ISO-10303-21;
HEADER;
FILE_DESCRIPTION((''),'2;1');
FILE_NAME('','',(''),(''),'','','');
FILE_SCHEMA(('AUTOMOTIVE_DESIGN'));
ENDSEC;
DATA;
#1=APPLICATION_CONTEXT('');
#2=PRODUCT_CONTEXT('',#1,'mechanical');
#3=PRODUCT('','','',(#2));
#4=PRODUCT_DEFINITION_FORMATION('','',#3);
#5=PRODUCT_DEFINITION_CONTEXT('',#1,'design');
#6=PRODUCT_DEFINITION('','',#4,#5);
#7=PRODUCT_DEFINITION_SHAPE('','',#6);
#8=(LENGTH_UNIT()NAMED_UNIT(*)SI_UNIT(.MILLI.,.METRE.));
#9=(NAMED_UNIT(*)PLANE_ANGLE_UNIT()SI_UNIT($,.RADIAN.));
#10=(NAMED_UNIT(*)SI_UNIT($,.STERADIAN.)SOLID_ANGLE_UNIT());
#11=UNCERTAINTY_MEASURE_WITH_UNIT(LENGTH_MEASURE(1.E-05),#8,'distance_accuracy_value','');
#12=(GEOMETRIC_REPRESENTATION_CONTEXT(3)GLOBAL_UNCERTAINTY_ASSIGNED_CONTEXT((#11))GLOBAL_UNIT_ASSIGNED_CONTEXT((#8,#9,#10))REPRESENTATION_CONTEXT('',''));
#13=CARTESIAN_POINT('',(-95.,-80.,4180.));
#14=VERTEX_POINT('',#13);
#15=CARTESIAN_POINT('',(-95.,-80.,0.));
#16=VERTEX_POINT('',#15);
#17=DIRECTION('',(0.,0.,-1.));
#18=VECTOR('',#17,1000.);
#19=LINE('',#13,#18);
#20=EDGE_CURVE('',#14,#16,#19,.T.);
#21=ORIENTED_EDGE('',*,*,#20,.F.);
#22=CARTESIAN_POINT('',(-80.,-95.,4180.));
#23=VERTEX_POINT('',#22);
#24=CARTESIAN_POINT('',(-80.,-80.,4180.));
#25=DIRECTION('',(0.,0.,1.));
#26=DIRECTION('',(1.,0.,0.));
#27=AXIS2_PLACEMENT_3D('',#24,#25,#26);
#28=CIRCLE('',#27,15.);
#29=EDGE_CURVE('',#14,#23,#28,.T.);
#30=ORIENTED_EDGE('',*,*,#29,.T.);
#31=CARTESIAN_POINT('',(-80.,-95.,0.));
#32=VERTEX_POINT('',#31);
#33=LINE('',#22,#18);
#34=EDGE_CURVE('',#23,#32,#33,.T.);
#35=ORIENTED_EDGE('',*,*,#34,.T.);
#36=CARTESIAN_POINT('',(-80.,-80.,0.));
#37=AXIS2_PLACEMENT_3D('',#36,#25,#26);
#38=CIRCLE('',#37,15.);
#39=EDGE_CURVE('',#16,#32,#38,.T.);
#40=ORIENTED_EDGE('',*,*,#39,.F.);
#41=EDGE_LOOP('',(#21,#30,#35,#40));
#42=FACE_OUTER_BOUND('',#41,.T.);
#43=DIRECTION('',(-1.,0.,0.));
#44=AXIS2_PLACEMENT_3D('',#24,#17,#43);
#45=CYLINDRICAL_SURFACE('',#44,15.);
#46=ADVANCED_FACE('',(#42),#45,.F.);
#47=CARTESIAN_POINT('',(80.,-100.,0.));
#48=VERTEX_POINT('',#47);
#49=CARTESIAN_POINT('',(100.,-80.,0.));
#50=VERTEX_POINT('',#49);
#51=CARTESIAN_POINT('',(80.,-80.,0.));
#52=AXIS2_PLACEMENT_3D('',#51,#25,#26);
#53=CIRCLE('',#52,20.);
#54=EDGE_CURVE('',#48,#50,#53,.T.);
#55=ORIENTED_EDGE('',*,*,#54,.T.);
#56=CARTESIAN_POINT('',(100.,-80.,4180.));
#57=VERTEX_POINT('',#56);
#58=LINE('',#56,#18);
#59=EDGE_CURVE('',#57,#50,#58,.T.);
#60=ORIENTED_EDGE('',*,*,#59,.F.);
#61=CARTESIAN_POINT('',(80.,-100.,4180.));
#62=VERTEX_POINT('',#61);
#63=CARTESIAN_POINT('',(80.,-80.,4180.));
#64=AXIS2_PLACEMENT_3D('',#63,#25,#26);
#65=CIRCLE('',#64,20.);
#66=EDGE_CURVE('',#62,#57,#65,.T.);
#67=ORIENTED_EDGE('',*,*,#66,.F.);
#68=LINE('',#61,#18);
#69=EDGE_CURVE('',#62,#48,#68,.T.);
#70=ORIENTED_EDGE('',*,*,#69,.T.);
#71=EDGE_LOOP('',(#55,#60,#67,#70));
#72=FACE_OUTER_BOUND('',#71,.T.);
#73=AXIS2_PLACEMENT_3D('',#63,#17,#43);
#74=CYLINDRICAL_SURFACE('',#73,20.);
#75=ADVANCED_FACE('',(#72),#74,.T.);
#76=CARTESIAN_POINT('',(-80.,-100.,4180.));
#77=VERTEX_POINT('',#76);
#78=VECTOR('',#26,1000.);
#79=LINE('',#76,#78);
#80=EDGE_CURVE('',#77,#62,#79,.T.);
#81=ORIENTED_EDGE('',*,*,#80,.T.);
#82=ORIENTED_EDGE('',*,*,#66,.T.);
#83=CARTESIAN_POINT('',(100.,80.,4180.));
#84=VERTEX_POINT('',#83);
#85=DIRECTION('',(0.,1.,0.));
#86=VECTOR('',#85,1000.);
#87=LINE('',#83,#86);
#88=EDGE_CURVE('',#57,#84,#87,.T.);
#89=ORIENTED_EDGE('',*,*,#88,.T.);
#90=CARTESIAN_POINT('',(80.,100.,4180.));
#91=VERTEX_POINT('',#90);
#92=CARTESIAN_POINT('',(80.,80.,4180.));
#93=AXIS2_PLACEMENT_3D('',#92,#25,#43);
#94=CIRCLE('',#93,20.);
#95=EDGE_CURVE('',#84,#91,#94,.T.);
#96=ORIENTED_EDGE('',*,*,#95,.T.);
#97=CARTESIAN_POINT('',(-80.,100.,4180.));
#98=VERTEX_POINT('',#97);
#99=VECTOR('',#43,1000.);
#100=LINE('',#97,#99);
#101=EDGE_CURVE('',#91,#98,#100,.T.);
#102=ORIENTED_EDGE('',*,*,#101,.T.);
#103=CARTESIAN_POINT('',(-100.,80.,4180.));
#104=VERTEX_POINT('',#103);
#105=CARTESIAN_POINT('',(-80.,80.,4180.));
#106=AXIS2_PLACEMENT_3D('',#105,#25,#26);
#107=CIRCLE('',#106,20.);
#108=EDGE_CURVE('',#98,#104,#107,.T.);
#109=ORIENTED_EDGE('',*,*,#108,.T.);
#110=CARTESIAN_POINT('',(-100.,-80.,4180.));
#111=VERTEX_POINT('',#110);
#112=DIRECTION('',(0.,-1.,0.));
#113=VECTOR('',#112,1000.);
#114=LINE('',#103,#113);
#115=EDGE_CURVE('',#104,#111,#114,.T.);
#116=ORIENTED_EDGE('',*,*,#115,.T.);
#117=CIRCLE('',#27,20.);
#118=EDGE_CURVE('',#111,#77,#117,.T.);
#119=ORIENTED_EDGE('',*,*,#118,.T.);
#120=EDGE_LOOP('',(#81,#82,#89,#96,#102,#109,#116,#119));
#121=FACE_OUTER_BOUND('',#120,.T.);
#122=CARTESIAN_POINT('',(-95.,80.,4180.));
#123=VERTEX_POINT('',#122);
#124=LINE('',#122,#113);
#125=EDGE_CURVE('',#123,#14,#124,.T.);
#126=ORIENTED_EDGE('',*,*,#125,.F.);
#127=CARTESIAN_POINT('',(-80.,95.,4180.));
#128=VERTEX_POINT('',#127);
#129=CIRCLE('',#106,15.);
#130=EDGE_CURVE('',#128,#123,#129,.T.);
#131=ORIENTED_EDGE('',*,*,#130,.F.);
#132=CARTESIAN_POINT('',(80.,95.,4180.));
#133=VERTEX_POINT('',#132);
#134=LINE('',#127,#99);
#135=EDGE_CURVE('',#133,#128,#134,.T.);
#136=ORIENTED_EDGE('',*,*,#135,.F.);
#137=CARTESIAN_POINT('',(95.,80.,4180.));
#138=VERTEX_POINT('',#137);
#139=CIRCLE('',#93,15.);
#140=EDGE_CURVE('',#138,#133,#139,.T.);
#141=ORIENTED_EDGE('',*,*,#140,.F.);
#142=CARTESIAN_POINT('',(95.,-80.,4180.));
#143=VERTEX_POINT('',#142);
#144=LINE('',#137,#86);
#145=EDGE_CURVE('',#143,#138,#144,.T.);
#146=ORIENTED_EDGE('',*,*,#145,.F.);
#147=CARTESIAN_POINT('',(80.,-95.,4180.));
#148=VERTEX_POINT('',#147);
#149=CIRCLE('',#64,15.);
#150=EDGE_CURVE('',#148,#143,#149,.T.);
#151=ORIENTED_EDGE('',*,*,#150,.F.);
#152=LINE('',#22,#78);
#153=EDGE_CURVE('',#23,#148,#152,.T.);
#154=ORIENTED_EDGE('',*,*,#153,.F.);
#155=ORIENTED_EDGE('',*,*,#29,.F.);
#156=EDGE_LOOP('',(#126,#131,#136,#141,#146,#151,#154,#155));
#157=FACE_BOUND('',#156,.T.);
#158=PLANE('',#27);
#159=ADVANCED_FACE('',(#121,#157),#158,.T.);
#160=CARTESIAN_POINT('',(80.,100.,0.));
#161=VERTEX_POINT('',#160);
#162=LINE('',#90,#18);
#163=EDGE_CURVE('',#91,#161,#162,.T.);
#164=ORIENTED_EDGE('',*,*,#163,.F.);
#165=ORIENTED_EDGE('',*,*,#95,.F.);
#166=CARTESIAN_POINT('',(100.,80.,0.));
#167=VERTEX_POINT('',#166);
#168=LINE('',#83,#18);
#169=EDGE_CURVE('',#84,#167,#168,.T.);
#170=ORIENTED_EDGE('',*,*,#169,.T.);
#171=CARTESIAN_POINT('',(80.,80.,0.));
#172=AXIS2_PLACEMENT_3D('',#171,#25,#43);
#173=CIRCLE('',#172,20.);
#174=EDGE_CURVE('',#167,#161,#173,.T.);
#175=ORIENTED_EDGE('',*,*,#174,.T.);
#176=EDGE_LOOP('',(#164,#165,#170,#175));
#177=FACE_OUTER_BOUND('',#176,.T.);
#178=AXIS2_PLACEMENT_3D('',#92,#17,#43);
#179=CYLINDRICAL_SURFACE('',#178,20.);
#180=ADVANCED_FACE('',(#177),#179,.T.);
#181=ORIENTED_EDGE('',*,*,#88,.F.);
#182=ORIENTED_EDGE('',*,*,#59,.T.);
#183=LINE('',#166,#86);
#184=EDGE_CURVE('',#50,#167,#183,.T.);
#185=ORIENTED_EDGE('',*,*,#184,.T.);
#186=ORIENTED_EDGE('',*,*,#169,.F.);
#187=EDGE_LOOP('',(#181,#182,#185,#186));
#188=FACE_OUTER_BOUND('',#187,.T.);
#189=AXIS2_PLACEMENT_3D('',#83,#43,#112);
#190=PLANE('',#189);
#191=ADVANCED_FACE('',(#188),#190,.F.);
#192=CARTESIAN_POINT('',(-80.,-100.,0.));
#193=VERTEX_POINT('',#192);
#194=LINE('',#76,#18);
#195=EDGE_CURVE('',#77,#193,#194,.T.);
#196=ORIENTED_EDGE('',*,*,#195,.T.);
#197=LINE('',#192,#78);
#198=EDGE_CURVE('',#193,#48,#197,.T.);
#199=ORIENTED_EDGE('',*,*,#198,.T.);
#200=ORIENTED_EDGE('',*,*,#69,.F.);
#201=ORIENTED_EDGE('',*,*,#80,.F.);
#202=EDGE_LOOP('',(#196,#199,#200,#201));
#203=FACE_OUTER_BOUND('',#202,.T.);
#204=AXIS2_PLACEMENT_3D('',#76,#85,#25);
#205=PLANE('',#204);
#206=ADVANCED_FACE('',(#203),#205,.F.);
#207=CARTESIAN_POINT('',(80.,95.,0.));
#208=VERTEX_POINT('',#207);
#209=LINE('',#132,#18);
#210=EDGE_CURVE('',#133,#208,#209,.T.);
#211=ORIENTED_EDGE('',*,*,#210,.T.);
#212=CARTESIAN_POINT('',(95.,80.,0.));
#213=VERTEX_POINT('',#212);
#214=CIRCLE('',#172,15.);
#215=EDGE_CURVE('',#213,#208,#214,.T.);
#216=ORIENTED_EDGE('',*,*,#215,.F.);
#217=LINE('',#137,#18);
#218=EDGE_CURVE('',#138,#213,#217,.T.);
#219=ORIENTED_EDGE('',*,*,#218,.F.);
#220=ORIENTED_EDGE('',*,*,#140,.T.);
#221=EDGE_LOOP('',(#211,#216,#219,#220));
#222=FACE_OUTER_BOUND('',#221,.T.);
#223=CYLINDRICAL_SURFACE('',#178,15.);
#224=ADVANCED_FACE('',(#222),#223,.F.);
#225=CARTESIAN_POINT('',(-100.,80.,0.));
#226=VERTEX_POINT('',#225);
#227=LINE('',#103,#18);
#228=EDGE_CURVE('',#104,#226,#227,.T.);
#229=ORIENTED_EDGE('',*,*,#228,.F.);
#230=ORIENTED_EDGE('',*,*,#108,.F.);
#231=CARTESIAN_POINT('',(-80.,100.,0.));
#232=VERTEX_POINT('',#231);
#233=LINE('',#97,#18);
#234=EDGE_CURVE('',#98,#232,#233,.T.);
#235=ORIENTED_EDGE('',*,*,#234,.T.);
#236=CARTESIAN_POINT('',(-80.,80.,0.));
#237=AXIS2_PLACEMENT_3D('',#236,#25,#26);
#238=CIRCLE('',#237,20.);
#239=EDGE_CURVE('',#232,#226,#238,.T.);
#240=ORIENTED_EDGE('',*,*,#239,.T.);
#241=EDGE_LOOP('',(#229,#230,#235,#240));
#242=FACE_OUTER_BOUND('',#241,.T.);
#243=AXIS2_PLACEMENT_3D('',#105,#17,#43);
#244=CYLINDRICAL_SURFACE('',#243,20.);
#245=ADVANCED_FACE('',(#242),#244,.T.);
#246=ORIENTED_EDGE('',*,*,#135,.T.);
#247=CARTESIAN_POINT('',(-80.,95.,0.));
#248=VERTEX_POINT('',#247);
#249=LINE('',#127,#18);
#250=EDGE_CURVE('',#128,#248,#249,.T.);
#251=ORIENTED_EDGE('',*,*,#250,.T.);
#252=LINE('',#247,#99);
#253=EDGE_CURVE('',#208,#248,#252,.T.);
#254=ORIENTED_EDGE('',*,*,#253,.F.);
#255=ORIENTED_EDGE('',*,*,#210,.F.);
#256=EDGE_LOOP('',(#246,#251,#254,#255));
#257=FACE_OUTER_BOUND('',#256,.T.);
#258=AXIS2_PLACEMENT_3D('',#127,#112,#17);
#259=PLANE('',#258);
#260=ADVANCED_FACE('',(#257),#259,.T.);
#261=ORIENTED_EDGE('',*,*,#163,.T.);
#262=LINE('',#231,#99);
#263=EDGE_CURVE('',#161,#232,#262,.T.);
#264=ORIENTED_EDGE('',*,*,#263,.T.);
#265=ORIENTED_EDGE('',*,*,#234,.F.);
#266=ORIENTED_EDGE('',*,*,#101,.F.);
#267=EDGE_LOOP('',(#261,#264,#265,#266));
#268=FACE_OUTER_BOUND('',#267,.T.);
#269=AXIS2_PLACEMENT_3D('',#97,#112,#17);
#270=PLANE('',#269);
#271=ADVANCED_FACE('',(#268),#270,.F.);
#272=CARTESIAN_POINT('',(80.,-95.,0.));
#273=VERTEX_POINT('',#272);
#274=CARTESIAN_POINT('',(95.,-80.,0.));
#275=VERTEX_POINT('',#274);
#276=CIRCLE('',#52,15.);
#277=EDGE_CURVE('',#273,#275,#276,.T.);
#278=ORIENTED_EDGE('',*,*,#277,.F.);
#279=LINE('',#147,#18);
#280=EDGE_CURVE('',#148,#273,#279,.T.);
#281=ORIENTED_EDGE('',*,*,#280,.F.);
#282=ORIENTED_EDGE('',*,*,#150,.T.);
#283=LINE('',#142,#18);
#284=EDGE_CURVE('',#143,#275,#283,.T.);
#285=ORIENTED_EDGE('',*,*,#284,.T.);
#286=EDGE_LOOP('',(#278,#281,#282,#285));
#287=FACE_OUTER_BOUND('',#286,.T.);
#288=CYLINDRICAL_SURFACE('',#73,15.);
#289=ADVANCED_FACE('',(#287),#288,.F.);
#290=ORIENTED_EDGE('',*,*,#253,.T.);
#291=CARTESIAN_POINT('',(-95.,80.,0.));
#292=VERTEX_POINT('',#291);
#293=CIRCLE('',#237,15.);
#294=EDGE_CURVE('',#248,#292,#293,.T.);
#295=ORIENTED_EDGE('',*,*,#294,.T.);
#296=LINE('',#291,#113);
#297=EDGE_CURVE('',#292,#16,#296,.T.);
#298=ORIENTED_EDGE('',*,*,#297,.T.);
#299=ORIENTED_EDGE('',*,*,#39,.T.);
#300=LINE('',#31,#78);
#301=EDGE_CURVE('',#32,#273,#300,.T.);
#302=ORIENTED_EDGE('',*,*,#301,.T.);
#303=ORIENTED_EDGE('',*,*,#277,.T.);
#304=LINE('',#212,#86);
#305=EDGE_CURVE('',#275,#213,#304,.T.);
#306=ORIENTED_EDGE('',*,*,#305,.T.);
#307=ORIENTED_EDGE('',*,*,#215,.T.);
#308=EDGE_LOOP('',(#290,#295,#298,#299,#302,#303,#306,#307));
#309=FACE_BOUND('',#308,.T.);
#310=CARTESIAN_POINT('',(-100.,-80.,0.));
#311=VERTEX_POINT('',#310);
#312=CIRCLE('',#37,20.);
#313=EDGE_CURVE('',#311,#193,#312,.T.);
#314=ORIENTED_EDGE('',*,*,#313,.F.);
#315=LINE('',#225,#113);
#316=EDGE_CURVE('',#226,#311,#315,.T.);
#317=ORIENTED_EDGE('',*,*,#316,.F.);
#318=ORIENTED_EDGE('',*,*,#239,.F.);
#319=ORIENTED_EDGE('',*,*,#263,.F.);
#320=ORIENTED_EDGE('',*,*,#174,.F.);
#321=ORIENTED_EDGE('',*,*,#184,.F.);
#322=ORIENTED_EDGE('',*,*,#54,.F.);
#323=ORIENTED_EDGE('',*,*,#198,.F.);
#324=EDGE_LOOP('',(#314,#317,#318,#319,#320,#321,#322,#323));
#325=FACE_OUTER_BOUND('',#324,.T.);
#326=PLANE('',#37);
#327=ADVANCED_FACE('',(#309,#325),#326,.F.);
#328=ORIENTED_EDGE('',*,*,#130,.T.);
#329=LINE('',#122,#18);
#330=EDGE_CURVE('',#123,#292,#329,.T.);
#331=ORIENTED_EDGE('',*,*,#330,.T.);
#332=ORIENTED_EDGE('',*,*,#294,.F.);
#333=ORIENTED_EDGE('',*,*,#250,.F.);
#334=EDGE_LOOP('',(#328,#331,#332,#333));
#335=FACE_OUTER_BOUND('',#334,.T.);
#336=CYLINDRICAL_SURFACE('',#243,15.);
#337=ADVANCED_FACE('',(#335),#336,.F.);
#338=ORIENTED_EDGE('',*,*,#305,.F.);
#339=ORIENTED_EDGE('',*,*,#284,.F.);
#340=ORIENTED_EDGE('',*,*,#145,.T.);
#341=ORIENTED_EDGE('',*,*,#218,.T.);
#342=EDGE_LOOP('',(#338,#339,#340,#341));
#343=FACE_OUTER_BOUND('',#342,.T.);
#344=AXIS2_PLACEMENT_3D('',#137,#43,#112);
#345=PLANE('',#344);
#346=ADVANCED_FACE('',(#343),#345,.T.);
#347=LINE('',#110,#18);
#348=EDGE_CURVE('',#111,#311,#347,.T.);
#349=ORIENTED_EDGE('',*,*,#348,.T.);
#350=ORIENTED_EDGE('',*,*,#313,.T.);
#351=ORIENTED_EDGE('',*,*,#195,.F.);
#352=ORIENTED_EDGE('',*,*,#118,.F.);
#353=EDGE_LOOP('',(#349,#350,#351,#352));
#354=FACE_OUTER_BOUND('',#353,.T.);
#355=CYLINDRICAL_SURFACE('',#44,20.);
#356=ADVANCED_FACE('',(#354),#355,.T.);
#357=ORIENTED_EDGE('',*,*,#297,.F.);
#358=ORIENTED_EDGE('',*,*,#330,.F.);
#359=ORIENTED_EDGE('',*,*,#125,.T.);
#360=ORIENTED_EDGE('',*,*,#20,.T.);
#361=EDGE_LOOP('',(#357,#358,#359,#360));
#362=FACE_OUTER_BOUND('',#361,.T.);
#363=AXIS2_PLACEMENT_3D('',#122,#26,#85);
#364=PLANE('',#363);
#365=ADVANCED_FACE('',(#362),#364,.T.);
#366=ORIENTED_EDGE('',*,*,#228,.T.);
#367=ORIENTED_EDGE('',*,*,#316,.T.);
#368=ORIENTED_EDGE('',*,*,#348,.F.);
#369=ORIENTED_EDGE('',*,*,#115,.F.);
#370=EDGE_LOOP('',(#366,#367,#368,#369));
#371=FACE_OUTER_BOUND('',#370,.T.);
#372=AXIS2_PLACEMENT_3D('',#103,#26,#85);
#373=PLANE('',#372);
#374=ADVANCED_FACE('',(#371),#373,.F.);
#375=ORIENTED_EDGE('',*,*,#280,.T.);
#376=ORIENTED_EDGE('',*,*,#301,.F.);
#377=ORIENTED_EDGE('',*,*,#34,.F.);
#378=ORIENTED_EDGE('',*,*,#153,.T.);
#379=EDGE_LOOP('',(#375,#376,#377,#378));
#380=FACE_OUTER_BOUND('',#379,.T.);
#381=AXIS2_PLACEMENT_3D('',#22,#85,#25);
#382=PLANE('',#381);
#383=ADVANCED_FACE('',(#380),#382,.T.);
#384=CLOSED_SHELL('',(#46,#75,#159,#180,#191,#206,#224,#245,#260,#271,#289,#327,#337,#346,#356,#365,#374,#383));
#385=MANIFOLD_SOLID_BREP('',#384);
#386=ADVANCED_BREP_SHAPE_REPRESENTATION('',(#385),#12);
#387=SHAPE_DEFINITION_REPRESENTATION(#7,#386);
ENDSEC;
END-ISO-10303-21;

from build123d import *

# Parameters (mm, degrees)
BOSS_EXTRUDE1_DEPTH = 4180


with BuildPart() as part:
    # Sketch1 → Boss-Extrude1 (new body)
    with BuildSketch(Plane.XY):
        with BuildLine():
            Line((-80, 100), (80, 100))
            ThreePointArc((80, 100), (94.142135624, 94.142135624), (100, 80))
            Line((100, 80), (100, -80))
            ThreePointArc((100, -80), (94.142135624, -94.142135624), (80, -100))
            Line((80, -100), (-80, -100))
            ThreePointArc((-80, -100), (-94.142135624, -94.142135624), (-100, -80))
            Line((-100, -80), (-100, 80))
            ThreePointArc((-100, 80), (-94.142135624, 94.142135624), (-80, 100))
        make_face()
        with BuildLine():
            Line((-95, 80), (-95, -80))
            ThreePointArc((-95, -80), (-90.606601718, -90.606601718), (-80, -95))
            Line((-80, -95), (80, -95))
            ThreePointArc((80, -95), (90.606601718, -90.606601718), (95, -80))
            Line((95, -80), (95, 80))
            ThreePointArc((95, 80), (90.606601718, 90.606601718), (80, 95))
            Line((80, 95), (-80, 95))
            ThreePointArc((-80, 95), (-90.606601718, 90.606601718), (-95, 80))
        make_face(mode=Mode.SUBTRACT)
    extrude(amount=BOSS_EXTRUDE1_DEPTH)


solid = part.part
